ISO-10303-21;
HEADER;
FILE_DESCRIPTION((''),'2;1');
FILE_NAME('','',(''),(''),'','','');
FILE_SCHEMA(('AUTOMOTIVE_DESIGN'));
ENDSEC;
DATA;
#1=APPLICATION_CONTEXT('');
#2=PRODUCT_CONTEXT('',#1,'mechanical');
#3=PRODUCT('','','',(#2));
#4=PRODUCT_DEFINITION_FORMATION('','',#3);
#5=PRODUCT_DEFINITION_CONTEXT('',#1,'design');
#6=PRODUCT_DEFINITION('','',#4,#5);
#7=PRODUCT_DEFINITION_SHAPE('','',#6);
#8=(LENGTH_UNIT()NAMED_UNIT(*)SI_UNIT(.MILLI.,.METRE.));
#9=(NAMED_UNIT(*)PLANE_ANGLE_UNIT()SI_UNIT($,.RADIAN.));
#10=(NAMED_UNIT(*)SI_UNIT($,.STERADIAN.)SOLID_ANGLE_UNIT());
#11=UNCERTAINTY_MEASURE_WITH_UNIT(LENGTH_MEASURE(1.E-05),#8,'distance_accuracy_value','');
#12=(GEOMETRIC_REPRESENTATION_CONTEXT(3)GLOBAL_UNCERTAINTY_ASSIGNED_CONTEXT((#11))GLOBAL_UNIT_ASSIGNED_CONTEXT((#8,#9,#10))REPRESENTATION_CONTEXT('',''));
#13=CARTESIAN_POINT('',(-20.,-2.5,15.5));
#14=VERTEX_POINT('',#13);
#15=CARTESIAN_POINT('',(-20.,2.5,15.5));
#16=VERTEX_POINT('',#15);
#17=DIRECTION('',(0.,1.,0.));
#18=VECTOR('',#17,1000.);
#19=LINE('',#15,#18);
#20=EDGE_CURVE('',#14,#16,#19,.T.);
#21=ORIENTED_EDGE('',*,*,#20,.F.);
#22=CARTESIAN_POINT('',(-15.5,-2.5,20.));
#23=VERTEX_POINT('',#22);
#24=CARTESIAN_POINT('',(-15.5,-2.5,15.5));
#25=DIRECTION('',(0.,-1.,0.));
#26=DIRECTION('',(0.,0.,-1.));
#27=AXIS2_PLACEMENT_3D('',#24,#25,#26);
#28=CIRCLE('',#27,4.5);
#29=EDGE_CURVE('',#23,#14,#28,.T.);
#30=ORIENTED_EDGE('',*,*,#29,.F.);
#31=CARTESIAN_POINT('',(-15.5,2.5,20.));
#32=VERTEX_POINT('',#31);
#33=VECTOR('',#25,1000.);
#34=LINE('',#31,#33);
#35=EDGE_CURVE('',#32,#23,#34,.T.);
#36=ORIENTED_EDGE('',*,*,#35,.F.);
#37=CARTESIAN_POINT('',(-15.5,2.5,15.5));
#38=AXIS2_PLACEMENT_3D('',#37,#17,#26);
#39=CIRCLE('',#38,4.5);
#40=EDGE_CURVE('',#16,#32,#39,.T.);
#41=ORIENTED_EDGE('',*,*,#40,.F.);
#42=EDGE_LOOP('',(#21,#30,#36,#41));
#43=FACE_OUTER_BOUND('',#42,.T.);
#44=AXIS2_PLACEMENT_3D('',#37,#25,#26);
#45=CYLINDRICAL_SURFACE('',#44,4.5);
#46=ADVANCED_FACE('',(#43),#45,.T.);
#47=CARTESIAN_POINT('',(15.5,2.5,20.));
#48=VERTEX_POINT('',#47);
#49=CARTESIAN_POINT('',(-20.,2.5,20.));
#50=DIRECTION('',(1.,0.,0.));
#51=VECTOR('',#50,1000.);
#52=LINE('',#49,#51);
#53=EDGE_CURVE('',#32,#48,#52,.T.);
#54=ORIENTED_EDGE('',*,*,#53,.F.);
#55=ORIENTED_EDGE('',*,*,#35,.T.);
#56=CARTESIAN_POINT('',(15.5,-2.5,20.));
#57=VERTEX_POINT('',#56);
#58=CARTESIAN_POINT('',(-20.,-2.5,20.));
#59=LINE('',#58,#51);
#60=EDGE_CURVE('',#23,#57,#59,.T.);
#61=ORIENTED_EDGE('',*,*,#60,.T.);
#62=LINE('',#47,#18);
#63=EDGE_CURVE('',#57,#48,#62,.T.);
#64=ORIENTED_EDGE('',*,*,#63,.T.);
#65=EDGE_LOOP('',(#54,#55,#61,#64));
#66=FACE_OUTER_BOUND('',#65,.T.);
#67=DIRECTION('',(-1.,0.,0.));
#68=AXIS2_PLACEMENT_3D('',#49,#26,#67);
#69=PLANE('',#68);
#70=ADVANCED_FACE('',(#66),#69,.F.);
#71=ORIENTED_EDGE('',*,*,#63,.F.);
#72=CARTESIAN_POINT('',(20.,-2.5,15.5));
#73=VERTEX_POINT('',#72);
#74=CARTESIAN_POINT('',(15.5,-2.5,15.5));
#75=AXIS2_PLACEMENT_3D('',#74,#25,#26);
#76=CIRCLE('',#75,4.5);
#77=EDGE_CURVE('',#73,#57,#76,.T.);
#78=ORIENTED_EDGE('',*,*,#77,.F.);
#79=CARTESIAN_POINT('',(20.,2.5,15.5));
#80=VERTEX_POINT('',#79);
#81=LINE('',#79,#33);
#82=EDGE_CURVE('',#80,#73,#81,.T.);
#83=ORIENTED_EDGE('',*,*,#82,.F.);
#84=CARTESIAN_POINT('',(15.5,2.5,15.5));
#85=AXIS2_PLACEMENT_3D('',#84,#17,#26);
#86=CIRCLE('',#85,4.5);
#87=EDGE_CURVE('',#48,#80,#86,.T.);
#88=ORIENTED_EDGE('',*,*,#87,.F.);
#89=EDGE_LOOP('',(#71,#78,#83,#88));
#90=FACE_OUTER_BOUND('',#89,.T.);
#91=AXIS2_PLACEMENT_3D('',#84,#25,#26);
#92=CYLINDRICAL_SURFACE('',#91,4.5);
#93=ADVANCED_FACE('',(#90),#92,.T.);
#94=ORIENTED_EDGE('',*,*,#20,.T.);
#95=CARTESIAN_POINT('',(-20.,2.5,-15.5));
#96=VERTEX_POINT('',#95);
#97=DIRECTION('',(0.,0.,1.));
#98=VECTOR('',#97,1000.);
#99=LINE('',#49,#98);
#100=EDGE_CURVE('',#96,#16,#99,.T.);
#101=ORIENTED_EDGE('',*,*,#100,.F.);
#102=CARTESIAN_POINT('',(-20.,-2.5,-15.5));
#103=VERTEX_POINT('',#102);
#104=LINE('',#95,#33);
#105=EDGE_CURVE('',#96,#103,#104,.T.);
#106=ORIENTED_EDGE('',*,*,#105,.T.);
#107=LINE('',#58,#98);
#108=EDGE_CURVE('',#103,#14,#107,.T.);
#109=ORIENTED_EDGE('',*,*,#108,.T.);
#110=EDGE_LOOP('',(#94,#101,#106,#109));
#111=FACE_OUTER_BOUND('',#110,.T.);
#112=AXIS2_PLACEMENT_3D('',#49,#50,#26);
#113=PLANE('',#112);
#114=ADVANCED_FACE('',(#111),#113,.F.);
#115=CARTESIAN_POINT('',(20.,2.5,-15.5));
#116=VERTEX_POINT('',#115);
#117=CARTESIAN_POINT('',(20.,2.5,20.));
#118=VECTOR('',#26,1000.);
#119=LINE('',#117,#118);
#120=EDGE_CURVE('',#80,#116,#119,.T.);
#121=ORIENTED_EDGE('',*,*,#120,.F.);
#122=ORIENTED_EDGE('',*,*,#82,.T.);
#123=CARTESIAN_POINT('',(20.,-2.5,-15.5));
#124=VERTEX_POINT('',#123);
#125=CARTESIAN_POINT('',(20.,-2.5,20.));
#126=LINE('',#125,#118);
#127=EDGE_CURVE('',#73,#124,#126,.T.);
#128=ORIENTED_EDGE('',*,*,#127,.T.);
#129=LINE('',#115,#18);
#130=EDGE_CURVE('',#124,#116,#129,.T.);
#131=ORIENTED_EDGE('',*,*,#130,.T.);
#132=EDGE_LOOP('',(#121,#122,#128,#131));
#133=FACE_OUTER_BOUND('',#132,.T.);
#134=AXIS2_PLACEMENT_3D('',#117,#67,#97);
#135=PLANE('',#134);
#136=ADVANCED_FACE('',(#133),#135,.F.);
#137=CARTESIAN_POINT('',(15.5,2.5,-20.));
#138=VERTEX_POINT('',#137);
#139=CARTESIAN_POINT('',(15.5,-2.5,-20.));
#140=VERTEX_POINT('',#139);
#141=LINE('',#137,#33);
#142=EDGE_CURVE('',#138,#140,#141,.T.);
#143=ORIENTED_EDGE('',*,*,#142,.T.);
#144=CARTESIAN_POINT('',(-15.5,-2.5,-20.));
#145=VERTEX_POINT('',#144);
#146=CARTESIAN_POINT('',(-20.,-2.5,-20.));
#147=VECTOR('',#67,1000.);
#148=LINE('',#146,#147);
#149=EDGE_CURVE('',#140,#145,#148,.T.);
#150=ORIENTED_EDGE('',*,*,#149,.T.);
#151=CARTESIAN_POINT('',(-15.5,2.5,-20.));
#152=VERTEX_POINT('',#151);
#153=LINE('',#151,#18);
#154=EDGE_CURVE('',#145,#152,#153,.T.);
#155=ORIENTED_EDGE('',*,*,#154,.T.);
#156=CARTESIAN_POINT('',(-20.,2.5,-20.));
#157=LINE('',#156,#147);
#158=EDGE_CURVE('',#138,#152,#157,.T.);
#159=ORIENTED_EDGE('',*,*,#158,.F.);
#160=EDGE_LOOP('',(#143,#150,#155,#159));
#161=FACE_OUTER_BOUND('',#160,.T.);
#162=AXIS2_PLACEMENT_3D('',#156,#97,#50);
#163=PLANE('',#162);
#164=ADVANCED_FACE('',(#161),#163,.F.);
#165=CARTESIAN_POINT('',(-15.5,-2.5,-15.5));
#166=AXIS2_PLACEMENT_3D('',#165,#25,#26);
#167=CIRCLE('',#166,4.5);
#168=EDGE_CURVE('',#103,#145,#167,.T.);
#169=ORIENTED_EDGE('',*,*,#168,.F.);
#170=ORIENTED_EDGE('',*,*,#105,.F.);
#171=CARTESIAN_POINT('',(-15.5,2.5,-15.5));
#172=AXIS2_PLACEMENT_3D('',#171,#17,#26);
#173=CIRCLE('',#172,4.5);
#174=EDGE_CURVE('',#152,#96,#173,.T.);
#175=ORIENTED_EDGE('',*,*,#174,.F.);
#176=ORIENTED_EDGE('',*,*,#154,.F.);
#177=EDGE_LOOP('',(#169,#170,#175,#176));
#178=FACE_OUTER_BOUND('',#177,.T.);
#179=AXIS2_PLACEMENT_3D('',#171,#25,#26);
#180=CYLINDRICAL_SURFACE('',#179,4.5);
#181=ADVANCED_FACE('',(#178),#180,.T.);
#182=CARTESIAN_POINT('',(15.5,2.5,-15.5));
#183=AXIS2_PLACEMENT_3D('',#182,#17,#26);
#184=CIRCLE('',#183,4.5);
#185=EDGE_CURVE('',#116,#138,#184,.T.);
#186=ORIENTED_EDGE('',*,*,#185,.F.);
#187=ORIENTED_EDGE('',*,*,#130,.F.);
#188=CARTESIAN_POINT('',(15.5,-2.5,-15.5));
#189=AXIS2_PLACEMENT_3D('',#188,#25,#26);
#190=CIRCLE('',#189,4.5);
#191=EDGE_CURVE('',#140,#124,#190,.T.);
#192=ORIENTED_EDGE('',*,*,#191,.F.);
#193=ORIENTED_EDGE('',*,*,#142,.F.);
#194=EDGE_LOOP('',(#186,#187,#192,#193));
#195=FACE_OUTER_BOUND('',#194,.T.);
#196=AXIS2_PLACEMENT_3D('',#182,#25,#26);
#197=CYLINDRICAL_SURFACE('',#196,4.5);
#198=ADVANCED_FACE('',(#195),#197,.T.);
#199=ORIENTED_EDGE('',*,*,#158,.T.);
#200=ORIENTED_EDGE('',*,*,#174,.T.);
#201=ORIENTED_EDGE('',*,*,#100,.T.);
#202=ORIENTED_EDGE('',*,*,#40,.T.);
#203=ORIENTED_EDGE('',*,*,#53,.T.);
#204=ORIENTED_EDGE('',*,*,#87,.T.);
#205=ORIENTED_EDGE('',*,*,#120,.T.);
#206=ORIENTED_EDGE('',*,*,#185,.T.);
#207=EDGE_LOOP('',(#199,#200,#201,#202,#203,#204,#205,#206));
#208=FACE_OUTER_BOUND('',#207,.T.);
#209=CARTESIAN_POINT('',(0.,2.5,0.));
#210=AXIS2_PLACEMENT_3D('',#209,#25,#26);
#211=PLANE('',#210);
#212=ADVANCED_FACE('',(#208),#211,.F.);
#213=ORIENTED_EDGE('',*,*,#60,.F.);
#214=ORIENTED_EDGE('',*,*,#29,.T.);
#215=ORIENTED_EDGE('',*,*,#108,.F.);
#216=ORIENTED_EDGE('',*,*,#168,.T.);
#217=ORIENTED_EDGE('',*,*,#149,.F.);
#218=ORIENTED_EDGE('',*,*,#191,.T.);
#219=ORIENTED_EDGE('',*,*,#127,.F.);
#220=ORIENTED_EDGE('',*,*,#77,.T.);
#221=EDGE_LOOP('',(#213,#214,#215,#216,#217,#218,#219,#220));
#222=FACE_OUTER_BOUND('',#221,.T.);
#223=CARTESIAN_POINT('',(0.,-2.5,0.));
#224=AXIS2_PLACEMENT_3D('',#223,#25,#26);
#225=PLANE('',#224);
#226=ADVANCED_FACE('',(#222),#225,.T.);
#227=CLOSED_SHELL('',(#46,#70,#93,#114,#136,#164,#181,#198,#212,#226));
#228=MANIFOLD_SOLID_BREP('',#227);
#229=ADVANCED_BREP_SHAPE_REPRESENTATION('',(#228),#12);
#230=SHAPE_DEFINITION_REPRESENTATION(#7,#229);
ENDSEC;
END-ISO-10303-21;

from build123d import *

# Parameters (mm, degrees)
SKETCH_1_W      = 40
SKETCH_1_H      = 40
EXTRUDE_1_DEPTH = 2.5
FILLET_1_R      = 4.5


with BuildPart() as part:
    # 草图1 → 凸台-拉伸1 (new, symmetric)
    with BuildSketch(Plane(origin=(0, 0, 0), x_dir=(1, 0, 0), z_dir=(0, 1, 0))):
        Rectangle(SKETCH_1_W, SKETCH_1_H)
    extrude(amount=EXTRUDE_1_DEPTH, both=True)

    # 圆角1
    fillet_1_edges = [part.edges().sort_by_distance(p)[0] for p in [
        (20, 0, 20),
        (-20, 0, 20),
        (-20, 0, -20),
        (20, 0, -20),
    ]]
    fillet(fillet_1_edges, radius=FILLET_1_R)


solid = part.part
